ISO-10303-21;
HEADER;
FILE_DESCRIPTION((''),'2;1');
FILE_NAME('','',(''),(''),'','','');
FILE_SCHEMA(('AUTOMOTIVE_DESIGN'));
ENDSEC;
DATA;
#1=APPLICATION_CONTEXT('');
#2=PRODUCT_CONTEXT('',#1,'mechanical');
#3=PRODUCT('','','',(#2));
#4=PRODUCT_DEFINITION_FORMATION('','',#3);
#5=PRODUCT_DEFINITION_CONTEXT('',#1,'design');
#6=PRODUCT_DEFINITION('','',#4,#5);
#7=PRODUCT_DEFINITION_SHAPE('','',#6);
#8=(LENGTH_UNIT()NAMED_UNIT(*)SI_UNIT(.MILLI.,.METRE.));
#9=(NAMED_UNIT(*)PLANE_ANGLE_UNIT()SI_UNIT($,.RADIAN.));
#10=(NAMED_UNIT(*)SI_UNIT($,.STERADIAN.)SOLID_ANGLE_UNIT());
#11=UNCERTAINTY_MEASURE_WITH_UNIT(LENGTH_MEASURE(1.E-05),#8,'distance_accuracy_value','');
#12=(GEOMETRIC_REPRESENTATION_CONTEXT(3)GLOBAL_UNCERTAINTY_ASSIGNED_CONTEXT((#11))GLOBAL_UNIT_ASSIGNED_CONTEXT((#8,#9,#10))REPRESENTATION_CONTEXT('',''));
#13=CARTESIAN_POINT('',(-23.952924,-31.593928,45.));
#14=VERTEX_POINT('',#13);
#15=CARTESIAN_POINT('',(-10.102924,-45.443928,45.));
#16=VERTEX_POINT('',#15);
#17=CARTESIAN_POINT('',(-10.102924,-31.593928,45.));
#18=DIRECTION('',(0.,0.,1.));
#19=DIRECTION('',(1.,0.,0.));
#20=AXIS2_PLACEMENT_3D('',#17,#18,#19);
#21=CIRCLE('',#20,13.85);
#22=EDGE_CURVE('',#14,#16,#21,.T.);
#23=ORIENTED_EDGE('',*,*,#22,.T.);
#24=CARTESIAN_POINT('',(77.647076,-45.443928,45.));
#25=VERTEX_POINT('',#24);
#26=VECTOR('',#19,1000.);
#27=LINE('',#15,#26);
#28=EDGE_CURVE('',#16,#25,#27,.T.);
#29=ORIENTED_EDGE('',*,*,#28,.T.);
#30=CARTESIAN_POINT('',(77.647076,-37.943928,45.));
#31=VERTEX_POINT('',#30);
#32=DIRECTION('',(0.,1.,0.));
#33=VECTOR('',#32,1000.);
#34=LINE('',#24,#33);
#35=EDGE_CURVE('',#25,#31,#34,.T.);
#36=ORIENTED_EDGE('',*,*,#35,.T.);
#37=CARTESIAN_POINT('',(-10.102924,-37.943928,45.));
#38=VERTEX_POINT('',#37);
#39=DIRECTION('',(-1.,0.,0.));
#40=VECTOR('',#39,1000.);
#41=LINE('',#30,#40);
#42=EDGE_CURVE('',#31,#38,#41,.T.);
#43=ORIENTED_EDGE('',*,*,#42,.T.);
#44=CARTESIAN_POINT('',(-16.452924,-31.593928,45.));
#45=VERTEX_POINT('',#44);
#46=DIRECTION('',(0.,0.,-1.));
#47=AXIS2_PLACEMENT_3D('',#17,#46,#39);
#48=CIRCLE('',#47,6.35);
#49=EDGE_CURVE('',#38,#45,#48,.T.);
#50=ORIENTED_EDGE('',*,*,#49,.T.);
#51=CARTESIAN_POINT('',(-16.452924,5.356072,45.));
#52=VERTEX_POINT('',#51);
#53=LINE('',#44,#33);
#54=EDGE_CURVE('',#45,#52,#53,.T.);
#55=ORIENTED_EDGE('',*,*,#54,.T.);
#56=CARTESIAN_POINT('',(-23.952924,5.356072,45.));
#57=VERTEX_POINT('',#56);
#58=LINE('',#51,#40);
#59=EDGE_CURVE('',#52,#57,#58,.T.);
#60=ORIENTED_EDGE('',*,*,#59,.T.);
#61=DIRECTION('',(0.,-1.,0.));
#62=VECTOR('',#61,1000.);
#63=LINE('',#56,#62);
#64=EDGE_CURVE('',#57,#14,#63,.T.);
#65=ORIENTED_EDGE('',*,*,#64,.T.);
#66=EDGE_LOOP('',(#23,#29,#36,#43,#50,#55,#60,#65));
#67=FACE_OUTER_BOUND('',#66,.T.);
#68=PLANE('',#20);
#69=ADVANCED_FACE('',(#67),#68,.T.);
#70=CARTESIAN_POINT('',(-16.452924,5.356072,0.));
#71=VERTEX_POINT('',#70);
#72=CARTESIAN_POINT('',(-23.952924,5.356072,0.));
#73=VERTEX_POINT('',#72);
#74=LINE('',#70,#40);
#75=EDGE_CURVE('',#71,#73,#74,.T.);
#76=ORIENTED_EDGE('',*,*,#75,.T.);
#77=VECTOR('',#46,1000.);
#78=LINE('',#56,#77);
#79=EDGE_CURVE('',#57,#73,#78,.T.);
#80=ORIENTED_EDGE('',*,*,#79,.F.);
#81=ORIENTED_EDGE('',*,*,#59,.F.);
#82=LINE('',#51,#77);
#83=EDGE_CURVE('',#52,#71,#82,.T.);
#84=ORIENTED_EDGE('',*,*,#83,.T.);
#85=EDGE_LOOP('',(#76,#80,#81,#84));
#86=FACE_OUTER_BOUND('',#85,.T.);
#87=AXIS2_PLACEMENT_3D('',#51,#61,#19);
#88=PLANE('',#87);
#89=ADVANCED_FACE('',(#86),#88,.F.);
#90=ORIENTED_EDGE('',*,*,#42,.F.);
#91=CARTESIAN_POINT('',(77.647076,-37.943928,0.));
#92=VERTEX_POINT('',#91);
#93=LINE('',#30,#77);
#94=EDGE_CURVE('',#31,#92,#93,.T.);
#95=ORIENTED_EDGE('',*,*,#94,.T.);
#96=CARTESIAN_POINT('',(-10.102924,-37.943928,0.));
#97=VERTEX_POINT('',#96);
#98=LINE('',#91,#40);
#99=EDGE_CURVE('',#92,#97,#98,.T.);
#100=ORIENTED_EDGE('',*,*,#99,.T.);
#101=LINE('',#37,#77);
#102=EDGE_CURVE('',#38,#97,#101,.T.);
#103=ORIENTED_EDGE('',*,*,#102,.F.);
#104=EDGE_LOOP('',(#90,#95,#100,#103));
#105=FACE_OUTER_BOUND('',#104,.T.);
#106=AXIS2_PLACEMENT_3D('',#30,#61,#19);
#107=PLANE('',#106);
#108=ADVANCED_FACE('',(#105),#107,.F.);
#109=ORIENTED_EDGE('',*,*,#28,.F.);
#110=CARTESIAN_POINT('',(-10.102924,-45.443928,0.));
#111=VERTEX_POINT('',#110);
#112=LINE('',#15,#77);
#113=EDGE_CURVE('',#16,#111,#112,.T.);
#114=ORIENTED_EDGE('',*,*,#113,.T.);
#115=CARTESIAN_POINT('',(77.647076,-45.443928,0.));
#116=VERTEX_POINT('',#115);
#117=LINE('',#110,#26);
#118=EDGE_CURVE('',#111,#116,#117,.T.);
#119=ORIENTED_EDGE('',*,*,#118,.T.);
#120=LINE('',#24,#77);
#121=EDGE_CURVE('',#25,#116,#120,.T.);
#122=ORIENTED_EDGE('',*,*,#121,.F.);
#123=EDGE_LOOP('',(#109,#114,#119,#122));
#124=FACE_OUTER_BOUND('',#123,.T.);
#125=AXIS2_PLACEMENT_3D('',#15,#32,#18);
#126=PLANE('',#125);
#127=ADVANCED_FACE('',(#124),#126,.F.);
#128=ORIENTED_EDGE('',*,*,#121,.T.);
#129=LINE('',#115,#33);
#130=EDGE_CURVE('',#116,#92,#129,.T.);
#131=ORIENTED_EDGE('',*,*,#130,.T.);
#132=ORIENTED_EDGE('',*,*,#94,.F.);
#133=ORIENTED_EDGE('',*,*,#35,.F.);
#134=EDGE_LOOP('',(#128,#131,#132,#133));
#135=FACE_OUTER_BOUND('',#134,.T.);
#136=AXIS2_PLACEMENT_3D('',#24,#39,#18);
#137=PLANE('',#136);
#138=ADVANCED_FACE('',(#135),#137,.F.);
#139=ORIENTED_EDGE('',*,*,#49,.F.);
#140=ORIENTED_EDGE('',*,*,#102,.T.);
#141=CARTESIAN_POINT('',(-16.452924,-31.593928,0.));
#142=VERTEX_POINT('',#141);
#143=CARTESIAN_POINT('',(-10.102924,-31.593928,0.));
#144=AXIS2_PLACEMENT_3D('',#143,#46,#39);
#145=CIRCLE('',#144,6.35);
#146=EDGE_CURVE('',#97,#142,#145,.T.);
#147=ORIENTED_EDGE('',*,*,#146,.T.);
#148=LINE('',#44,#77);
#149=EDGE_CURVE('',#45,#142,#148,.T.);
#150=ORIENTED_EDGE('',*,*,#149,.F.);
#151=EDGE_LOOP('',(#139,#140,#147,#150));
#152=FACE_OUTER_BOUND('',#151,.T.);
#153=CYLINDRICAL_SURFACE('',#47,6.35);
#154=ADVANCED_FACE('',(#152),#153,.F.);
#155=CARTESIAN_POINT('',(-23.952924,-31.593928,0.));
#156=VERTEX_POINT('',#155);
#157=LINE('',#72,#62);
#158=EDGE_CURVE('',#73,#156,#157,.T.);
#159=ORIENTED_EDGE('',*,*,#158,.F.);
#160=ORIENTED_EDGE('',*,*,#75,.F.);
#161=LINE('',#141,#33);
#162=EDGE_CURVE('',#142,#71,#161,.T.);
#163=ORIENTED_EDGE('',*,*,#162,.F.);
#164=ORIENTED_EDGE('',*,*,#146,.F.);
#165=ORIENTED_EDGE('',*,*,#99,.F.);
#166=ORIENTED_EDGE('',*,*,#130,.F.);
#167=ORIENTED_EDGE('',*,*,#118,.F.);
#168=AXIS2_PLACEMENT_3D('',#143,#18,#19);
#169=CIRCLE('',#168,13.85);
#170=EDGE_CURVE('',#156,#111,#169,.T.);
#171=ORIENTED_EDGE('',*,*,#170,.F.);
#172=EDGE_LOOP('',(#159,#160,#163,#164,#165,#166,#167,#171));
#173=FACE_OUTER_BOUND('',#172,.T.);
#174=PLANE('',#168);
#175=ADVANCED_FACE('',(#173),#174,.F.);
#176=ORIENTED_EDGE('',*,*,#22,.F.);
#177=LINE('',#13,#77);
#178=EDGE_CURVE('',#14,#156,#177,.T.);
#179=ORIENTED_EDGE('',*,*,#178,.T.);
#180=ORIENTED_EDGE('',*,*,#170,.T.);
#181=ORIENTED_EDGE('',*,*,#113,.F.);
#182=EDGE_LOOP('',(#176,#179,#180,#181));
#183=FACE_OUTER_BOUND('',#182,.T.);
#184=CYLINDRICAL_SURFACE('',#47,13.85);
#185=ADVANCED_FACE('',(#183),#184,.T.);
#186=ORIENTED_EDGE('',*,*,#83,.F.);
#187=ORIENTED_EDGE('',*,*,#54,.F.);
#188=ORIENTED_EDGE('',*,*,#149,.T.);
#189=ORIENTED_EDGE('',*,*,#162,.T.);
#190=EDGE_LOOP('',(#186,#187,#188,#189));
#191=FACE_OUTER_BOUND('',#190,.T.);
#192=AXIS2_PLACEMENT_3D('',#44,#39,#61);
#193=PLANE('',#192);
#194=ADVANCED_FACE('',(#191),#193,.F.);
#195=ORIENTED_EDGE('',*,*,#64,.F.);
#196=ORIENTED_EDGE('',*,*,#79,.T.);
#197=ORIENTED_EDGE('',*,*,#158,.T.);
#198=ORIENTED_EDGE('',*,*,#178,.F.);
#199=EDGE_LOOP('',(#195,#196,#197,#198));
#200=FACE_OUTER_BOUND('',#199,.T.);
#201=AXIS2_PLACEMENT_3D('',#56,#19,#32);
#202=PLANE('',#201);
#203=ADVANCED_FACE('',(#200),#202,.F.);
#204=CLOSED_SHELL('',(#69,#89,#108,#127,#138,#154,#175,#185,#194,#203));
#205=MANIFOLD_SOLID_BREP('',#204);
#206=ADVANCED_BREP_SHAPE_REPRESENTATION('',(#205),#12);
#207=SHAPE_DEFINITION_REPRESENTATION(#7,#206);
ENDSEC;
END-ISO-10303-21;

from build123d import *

# Parameters (mm, degrees)
EXTRUDE1_DEPTH = 45


with BuildPart() as part:
    # Sketch1 → Extrude1 (new body)
    with BuildSketch(Plane.XY):
        with BuildLine():
            Line((-23.952923538, 5.356071964), (-23.952923538, -31.593928036))
            ThreePointArc((-23.952923538, -31.593928036), (-19.896352458, -41.387356955), (-10.102923538, -45.443928036))
            Line((-10.102923538, -45.443928036), (77.647076462, -45.443928036))
            Line((77.647076462, -45.443928036), (77.647076462, -37.943928036))
            Line((77.647076462, -37.943928036), (-10.102923538, -37.943928036))
            ThreePointArc((-10.102923538, -37.943928036), (-14.593051599, -36.084056097), (-16.452923538, -31.593928036))
            Line((-16.452923538, -31.593928036), (-16.452923538, 5.356071964))
            Line((-16.452923538, 5.356071964), (-23.952923538, 5.356071964))
        make_face()
    extrude(amount=EXTRUDE1_DEPTH)


solid = part.part
